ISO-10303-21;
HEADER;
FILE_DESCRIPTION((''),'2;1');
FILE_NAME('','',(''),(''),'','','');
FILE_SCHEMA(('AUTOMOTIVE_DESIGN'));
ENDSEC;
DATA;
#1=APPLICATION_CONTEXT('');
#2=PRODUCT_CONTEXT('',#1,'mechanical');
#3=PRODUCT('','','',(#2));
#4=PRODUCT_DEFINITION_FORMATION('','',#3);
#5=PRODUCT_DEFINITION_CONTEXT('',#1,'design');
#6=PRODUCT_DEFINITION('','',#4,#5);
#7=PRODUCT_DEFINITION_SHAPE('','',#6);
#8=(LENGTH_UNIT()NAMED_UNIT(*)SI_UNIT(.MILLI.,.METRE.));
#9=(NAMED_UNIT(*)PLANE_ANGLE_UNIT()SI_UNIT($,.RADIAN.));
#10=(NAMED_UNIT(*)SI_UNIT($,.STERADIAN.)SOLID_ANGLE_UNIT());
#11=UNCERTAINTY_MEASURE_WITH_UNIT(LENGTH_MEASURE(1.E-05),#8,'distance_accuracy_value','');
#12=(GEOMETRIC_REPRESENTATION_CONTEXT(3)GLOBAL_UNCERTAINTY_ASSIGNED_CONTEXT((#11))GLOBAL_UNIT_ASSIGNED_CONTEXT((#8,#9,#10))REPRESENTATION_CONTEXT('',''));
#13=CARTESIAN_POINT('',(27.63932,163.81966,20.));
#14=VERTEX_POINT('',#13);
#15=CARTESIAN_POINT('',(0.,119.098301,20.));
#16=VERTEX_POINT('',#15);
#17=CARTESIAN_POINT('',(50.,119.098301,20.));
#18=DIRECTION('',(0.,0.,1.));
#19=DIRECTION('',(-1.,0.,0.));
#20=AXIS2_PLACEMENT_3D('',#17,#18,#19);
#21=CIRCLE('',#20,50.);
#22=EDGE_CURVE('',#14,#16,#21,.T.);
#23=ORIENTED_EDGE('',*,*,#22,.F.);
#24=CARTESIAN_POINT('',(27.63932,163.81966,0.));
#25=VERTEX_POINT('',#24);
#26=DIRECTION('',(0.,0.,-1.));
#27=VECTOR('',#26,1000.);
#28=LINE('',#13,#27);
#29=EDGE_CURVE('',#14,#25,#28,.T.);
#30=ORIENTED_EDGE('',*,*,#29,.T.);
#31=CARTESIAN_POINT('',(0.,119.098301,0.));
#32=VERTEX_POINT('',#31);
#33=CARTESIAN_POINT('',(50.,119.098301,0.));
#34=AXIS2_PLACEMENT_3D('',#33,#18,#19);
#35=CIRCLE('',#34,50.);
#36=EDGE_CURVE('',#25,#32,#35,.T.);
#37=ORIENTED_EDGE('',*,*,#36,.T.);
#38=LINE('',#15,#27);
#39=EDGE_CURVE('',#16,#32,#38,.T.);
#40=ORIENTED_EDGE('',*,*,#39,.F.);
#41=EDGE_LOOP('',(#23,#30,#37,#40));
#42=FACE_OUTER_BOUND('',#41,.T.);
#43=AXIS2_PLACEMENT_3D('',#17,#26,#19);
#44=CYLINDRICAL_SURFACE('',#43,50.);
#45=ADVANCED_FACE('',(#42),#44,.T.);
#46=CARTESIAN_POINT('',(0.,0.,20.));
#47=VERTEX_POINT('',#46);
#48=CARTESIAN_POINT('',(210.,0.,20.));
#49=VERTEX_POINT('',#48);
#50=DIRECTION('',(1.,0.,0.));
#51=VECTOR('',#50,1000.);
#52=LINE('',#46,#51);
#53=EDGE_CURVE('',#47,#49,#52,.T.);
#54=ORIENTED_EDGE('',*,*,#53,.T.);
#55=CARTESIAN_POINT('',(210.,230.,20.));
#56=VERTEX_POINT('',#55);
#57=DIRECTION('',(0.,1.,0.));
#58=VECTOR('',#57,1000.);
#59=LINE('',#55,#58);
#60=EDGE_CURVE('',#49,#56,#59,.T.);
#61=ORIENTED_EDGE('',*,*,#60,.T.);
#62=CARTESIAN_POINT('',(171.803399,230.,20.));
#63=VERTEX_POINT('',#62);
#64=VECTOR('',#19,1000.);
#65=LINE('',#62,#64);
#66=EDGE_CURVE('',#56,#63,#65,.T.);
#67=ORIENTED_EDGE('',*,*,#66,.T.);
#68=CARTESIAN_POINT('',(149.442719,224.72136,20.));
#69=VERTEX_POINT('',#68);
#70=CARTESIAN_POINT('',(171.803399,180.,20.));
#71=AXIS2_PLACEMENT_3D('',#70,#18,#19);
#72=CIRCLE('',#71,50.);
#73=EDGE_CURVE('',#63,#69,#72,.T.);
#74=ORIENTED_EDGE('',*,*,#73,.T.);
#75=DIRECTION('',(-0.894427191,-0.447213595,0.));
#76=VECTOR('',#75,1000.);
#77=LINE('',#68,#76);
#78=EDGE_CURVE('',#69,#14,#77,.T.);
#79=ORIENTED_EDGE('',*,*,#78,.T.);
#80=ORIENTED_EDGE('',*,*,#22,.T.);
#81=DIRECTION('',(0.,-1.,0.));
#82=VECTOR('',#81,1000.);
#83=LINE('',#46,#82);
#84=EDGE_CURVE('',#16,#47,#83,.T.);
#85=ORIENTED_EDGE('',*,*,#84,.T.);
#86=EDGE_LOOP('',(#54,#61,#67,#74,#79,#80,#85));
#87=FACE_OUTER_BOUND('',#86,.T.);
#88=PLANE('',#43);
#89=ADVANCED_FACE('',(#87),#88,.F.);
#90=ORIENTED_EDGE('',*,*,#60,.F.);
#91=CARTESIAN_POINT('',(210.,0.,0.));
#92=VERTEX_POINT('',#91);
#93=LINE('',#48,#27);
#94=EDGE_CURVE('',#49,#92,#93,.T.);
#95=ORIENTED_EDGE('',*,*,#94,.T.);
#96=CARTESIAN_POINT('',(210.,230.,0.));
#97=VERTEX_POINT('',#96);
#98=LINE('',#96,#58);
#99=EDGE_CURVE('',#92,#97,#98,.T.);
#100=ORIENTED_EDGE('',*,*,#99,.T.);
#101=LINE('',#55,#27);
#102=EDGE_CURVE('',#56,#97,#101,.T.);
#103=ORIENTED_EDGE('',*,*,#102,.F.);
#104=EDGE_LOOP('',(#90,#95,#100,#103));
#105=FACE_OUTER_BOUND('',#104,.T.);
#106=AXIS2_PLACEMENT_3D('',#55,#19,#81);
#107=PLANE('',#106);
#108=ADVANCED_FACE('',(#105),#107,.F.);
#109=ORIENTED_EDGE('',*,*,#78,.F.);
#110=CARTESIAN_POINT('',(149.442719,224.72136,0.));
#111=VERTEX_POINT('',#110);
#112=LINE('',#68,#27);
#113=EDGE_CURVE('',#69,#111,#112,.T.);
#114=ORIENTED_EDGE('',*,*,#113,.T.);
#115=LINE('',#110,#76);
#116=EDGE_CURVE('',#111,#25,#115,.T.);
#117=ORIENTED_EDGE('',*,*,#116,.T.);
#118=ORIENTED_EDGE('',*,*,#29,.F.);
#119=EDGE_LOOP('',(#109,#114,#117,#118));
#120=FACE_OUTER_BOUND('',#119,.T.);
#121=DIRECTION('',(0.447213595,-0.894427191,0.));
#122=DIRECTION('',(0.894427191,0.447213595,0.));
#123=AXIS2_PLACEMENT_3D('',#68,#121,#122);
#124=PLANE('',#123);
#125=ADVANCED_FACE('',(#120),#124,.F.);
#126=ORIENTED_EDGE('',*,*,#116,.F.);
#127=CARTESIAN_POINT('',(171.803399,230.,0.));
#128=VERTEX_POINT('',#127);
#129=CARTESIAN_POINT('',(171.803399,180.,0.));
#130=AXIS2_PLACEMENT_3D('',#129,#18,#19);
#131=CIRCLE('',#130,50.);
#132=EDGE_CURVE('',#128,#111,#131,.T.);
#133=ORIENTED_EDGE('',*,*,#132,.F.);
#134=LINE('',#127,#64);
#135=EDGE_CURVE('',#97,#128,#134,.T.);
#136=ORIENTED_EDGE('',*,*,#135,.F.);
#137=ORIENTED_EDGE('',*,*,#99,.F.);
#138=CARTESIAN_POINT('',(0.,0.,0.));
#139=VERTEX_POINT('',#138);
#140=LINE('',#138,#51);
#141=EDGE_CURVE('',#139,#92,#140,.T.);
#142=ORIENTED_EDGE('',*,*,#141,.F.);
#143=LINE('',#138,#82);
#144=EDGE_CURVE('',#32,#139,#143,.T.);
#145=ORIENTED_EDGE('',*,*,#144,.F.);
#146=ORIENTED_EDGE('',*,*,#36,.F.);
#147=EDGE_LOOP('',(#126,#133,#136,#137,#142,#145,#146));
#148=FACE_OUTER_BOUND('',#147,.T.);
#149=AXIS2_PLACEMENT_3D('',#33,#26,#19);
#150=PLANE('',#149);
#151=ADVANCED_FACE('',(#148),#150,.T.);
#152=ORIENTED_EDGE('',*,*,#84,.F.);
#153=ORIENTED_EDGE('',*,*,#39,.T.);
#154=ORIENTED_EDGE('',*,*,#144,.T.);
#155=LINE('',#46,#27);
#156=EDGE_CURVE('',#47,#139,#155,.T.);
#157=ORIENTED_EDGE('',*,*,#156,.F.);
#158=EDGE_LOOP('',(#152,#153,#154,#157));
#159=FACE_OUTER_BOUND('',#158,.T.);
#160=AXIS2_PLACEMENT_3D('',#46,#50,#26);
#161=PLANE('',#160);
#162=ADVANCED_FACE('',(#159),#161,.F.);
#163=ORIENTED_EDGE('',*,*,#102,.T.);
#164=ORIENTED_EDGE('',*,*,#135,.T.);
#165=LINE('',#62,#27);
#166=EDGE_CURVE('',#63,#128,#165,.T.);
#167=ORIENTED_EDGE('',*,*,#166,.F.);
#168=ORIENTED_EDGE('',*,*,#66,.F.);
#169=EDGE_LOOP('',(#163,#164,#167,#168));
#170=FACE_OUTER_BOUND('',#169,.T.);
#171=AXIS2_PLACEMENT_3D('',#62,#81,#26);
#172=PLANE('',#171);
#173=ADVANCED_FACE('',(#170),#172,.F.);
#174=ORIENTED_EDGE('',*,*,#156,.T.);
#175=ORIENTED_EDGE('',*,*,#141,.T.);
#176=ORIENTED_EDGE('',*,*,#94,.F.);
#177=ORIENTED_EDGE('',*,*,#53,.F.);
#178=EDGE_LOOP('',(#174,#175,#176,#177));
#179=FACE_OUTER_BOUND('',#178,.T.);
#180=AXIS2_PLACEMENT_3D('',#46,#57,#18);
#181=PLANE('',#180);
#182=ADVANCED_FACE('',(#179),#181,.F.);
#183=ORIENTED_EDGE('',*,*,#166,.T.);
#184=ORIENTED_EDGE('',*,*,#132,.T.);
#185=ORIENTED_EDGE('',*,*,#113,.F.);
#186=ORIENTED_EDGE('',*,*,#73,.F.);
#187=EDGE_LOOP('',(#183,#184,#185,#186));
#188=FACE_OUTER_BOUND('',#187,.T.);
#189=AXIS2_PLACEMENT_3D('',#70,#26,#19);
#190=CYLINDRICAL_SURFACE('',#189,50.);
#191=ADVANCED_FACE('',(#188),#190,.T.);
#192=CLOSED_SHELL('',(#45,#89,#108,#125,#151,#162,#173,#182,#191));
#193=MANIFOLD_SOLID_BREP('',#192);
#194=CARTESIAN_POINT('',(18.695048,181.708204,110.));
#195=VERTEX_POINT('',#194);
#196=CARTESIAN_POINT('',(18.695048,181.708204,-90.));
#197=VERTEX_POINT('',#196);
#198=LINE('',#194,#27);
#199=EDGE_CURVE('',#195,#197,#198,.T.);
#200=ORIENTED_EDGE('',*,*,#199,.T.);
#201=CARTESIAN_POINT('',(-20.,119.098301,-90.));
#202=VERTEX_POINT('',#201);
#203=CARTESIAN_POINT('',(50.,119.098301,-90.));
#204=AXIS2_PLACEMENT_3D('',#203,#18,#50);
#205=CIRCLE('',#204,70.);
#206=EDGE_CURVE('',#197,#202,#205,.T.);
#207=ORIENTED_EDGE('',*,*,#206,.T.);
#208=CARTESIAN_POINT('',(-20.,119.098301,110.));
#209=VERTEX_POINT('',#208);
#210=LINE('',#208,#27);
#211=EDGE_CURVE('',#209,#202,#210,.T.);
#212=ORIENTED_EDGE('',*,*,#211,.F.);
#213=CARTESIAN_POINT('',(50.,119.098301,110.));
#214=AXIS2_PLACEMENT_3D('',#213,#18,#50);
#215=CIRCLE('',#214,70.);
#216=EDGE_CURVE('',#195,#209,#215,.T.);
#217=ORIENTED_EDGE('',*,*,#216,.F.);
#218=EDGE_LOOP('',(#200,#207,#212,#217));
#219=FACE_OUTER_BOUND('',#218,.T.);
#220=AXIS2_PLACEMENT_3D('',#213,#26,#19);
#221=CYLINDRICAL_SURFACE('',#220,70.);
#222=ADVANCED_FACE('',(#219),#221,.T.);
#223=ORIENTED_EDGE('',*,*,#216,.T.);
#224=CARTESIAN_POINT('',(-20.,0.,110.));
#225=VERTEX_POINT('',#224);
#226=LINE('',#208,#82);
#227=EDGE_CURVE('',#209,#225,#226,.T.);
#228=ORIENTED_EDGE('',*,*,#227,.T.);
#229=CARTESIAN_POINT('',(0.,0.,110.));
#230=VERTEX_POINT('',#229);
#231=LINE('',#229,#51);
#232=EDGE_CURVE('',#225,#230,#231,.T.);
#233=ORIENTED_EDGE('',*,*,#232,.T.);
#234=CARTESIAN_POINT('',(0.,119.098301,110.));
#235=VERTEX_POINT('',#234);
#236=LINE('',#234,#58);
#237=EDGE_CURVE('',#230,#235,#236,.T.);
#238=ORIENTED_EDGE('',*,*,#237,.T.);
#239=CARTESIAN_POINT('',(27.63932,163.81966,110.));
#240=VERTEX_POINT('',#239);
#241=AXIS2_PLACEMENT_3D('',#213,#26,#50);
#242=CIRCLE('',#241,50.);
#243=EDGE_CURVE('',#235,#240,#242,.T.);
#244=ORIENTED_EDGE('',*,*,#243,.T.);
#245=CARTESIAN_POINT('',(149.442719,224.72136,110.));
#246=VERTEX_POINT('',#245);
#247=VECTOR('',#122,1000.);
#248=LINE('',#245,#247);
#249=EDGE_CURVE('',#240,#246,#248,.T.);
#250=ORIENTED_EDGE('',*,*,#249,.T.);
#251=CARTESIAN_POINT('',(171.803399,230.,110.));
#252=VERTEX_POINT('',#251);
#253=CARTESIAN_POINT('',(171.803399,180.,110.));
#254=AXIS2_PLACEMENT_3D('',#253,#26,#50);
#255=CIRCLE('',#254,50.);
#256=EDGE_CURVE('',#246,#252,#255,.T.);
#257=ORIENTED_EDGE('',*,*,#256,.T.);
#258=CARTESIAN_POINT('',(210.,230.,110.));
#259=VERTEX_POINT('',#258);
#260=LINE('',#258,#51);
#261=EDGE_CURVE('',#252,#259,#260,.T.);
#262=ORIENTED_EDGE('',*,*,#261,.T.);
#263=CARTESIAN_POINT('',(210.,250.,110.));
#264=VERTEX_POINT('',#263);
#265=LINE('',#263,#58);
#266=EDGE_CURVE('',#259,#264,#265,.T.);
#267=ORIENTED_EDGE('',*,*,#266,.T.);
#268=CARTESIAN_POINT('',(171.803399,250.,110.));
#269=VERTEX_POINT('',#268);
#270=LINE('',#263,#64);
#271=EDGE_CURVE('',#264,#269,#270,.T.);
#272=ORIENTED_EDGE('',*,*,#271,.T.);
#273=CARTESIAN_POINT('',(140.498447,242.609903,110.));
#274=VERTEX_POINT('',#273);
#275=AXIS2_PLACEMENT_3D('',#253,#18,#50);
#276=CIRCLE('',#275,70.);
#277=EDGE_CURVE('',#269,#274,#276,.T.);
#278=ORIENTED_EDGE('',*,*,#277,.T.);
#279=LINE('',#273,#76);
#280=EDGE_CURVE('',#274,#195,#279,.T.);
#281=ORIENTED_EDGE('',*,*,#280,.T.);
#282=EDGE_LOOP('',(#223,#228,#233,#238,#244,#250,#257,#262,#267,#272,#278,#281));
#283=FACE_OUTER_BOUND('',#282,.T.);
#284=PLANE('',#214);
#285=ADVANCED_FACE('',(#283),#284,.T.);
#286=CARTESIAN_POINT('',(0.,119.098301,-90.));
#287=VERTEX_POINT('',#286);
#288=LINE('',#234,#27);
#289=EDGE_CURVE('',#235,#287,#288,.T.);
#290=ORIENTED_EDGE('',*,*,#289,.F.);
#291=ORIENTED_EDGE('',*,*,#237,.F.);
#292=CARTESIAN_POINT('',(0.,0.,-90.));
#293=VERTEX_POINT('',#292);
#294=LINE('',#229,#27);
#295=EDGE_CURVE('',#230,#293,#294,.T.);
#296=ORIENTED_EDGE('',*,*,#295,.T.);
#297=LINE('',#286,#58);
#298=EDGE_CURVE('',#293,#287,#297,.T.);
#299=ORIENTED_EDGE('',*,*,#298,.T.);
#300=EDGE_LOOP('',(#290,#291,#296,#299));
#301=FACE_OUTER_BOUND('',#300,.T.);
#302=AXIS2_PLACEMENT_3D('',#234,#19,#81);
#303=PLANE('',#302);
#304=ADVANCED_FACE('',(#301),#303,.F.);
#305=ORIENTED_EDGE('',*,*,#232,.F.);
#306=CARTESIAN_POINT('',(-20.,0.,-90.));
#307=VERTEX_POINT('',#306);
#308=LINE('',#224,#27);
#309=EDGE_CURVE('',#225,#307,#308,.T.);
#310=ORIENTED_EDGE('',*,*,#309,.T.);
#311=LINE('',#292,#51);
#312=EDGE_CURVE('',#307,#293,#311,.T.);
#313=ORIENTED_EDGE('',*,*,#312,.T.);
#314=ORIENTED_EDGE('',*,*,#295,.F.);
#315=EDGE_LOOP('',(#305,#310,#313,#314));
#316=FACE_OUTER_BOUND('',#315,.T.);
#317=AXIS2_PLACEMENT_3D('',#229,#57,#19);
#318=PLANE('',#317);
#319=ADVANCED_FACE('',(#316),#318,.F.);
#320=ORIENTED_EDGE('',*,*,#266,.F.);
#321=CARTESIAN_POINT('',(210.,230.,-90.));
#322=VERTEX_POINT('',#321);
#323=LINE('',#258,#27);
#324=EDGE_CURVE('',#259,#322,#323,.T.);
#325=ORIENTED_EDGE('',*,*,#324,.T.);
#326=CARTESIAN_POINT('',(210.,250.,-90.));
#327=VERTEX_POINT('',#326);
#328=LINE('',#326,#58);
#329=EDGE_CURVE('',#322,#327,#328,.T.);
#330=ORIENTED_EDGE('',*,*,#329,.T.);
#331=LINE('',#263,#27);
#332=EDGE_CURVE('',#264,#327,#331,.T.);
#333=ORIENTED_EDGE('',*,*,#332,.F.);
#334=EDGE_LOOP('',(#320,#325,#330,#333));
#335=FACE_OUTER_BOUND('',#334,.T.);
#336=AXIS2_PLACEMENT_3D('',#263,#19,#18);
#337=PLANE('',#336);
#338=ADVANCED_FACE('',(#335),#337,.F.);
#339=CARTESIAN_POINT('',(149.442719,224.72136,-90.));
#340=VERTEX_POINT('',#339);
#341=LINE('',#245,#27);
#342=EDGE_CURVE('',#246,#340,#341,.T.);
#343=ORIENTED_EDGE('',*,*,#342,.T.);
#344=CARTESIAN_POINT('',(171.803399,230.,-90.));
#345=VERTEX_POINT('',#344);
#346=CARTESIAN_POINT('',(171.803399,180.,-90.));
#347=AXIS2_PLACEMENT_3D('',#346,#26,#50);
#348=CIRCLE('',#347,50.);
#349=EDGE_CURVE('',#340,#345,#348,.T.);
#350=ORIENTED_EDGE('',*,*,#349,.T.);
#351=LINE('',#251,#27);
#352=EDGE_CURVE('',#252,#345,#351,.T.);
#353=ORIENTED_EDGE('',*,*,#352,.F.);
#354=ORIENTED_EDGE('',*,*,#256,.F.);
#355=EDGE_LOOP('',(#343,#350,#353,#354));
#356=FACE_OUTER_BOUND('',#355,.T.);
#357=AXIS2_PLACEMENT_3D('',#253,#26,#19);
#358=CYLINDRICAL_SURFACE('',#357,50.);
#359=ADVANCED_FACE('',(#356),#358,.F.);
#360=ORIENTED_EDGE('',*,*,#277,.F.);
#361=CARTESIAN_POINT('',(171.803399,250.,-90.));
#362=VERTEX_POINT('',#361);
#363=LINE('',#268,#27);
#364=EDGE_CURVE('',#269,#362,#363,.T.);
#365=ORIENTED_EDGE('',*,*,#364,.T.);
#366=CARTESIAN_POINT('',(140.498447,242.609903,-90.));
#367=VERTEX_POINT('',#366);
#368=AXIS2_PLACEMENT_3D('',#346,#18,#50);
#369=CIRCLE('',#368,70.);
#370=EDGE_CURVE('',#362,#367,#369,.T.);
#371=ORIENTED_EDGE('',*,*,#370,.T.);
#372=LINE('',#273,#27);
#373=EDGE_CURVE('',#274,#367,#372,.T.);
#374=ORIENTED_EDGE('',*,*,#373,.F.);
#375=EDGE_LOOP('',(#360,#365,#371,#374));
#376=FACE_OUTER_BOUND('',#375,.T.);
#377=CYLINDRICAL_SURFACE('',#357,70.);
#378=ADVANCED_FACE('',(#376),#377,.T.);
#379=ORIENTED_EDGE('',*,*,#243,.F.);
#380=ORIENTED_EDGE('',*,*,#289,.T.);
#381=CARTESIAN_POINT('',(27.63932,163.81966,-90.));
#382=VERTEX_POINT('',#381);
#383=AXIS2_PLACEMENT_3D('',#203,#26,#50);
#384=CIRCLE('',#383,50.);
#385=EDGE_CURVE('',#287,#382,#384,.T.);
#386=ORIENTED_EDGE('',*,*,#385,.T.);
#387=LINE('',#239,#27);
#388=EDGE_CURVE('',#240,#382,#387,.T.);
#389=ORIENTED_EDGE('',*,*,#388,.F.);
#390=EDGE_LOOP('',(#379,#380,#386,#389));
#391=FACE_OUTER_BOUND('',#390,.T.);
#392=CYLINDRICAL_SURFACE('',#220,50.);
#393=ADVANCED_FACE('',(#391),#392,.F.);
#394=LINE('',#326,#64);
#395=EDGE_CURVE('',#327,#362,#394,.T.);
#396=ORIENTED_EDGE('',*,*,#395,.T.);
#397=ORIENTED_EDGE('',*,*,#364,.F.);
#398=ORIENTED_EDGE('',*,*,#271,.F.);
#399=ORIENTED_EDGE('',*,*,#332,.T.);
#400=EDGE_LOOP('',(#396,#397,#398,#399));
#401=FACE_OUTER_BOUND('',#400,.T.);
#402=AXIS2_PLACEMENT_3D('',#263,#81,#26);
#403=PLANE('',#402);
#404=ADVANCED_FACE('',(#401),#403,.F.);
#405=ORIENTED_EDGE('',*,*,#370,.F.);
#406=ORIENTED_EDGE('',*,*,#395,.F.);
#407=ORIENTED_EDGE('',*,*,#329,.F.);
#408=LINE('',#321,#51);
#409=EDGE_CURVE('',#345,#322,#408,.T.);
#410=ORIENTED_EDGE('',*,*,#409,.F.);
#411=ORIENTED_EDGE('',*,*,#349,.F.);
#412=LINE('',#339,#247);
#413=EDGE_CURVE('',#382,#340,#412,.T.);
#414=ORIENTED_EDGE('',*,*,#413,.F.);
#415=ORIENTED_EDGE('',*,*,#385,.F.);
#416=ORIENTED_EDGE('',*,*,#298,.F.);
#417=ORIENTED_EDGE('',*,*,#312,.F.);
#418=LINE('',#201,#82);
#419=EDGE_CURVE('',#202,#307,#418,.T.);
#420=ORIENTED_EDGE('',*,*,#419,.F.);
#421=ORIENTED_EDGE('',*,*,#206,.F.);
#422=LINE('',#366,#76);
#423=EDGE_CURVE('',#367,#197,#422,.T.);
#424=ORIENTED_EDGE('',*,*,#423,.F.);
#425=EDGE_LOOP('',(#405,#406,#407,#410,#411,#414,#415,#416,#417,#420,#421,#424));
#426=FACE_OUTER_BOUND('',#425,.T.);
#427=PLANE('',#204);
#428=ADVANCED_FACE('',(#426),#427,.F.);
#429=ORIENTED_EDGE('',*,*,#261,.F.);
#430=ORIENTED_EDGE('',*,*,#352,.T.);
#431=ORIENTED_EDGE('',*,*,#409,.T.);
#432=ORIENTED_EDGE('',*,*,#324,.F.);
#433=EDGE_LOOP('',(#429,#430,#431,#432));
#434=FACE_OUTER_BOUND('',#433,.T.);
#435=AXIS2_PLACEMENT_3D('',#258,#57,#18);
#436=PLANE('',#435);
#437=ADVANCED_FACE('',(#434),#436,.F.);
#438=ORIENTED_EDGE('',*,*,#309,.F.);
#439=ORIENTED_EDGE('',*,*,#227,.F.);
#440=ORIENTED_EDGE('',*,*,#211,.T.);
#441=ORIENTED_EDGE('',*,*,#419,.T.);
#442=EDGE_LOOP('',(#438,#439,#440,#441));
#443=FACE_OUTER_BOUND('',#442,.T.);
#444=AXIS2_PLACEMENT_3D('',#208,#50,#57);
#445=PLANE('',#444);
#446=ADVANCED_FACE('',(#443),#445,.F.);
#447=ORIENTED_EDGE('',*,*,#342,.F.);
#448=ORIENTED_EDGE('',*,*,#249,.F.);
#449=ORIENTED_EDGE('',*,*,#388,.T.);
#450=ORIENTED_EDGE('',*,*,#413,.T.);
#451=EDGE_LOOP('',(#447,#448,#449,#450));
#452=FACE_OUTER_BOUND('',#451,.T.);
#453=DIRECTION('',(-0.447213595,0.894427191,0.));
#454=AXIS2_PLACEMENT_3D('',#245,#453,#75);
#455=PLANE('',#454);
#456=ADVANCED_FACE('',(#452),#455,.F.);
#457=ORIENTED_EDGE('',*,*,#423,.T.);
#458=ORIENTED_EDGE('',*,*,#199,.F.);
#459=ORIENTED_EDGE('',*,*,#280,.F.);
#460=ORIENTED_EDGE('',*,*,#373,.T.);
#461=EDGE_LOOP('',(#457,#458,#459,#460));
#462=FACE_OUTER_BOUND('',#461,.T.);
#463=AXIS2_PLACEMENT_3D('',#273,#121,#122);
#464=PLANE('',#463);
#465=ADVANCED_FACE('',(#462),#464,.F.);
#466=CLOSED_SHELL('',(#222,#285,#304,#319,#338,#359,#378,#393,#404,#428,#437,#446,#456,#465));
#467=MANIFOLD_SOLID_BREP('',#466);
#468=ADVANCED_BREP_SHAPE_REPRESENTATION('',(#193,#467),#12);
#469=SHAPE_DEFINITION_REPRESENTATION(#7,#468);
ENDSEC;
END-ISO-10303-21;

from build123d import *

# Parameters (mm, degrees)
EXTRUDE_1_DEPTH = 20
EXTRUDE_2_DEPTH = 100


with BuildPart() as part:
    # 草图1 → 凸台-拉伸1 (new body)
    with BuildSketch(Plane.XY):
        with BuildLine():
            Line((0, 0), (210, 0))
            Line((210, 0), (210, 230))
            Line((210, 230), (171.803398875, 230))
            ThreePointArc((171.803398875, 230), (160.315752848, 228.662449473), (149.4427191, 224.72135955))
            Line((149.4427191, 224.72135955), (27.639320225, 163.819660113))
            ThreePointArc((27.639320225, 163.819660113), (7.467459582, 145.384856168), (0, 119.098300563))
            Line((0, 119.098300563), (0, 0))
        make_face()
    extrude(amount=EXTRUDE_1_DEPTH)


with BuildPart() as body_2:
    # 草图2 → 凸台-拉伸2 (new, symmetric)
    with BuildSketch(Plane.XY.offset(10)):
        with BuildLine():
            Line((210, 250), (171.803398875, 250))
            ThreePointArc((171.803398875, 250), (155.720694437, 248.127429263), (140.49844719, 242.60990337))
            Line((140.49844719, 242.60990337), (18.695048315, 181.708203932))
            ThreePointArc((18.695048315, 181.708203932), (-9.545556585, 155.899478411), (-20, 119.098300563))
            Line((-20, 119.098300563), (-20, 0))
            Line((-20, 0), (0, 0))
            Line((0, 0), (0, 119.098300563))
            ThreePointArc((0, 119.098300563), (7.467459582, 145.384856168), (27.639320225, 163.819660113))
            Line((27.639320225, 163.819660113), (149.4427191, 224.72135955))
            ThreePointArc((149.4427191, 224.72135955), (160.315752848, 228.662449473), (171.803398875, 230))
            Line((171.803398875, 230), (210, 230))
            Line((210, 230), (210, 250))
        make_face()
    extrude(amount=EXTRUDE_2_DEPTH, both=True)


solid = Compound([part.part, body_2.part])
